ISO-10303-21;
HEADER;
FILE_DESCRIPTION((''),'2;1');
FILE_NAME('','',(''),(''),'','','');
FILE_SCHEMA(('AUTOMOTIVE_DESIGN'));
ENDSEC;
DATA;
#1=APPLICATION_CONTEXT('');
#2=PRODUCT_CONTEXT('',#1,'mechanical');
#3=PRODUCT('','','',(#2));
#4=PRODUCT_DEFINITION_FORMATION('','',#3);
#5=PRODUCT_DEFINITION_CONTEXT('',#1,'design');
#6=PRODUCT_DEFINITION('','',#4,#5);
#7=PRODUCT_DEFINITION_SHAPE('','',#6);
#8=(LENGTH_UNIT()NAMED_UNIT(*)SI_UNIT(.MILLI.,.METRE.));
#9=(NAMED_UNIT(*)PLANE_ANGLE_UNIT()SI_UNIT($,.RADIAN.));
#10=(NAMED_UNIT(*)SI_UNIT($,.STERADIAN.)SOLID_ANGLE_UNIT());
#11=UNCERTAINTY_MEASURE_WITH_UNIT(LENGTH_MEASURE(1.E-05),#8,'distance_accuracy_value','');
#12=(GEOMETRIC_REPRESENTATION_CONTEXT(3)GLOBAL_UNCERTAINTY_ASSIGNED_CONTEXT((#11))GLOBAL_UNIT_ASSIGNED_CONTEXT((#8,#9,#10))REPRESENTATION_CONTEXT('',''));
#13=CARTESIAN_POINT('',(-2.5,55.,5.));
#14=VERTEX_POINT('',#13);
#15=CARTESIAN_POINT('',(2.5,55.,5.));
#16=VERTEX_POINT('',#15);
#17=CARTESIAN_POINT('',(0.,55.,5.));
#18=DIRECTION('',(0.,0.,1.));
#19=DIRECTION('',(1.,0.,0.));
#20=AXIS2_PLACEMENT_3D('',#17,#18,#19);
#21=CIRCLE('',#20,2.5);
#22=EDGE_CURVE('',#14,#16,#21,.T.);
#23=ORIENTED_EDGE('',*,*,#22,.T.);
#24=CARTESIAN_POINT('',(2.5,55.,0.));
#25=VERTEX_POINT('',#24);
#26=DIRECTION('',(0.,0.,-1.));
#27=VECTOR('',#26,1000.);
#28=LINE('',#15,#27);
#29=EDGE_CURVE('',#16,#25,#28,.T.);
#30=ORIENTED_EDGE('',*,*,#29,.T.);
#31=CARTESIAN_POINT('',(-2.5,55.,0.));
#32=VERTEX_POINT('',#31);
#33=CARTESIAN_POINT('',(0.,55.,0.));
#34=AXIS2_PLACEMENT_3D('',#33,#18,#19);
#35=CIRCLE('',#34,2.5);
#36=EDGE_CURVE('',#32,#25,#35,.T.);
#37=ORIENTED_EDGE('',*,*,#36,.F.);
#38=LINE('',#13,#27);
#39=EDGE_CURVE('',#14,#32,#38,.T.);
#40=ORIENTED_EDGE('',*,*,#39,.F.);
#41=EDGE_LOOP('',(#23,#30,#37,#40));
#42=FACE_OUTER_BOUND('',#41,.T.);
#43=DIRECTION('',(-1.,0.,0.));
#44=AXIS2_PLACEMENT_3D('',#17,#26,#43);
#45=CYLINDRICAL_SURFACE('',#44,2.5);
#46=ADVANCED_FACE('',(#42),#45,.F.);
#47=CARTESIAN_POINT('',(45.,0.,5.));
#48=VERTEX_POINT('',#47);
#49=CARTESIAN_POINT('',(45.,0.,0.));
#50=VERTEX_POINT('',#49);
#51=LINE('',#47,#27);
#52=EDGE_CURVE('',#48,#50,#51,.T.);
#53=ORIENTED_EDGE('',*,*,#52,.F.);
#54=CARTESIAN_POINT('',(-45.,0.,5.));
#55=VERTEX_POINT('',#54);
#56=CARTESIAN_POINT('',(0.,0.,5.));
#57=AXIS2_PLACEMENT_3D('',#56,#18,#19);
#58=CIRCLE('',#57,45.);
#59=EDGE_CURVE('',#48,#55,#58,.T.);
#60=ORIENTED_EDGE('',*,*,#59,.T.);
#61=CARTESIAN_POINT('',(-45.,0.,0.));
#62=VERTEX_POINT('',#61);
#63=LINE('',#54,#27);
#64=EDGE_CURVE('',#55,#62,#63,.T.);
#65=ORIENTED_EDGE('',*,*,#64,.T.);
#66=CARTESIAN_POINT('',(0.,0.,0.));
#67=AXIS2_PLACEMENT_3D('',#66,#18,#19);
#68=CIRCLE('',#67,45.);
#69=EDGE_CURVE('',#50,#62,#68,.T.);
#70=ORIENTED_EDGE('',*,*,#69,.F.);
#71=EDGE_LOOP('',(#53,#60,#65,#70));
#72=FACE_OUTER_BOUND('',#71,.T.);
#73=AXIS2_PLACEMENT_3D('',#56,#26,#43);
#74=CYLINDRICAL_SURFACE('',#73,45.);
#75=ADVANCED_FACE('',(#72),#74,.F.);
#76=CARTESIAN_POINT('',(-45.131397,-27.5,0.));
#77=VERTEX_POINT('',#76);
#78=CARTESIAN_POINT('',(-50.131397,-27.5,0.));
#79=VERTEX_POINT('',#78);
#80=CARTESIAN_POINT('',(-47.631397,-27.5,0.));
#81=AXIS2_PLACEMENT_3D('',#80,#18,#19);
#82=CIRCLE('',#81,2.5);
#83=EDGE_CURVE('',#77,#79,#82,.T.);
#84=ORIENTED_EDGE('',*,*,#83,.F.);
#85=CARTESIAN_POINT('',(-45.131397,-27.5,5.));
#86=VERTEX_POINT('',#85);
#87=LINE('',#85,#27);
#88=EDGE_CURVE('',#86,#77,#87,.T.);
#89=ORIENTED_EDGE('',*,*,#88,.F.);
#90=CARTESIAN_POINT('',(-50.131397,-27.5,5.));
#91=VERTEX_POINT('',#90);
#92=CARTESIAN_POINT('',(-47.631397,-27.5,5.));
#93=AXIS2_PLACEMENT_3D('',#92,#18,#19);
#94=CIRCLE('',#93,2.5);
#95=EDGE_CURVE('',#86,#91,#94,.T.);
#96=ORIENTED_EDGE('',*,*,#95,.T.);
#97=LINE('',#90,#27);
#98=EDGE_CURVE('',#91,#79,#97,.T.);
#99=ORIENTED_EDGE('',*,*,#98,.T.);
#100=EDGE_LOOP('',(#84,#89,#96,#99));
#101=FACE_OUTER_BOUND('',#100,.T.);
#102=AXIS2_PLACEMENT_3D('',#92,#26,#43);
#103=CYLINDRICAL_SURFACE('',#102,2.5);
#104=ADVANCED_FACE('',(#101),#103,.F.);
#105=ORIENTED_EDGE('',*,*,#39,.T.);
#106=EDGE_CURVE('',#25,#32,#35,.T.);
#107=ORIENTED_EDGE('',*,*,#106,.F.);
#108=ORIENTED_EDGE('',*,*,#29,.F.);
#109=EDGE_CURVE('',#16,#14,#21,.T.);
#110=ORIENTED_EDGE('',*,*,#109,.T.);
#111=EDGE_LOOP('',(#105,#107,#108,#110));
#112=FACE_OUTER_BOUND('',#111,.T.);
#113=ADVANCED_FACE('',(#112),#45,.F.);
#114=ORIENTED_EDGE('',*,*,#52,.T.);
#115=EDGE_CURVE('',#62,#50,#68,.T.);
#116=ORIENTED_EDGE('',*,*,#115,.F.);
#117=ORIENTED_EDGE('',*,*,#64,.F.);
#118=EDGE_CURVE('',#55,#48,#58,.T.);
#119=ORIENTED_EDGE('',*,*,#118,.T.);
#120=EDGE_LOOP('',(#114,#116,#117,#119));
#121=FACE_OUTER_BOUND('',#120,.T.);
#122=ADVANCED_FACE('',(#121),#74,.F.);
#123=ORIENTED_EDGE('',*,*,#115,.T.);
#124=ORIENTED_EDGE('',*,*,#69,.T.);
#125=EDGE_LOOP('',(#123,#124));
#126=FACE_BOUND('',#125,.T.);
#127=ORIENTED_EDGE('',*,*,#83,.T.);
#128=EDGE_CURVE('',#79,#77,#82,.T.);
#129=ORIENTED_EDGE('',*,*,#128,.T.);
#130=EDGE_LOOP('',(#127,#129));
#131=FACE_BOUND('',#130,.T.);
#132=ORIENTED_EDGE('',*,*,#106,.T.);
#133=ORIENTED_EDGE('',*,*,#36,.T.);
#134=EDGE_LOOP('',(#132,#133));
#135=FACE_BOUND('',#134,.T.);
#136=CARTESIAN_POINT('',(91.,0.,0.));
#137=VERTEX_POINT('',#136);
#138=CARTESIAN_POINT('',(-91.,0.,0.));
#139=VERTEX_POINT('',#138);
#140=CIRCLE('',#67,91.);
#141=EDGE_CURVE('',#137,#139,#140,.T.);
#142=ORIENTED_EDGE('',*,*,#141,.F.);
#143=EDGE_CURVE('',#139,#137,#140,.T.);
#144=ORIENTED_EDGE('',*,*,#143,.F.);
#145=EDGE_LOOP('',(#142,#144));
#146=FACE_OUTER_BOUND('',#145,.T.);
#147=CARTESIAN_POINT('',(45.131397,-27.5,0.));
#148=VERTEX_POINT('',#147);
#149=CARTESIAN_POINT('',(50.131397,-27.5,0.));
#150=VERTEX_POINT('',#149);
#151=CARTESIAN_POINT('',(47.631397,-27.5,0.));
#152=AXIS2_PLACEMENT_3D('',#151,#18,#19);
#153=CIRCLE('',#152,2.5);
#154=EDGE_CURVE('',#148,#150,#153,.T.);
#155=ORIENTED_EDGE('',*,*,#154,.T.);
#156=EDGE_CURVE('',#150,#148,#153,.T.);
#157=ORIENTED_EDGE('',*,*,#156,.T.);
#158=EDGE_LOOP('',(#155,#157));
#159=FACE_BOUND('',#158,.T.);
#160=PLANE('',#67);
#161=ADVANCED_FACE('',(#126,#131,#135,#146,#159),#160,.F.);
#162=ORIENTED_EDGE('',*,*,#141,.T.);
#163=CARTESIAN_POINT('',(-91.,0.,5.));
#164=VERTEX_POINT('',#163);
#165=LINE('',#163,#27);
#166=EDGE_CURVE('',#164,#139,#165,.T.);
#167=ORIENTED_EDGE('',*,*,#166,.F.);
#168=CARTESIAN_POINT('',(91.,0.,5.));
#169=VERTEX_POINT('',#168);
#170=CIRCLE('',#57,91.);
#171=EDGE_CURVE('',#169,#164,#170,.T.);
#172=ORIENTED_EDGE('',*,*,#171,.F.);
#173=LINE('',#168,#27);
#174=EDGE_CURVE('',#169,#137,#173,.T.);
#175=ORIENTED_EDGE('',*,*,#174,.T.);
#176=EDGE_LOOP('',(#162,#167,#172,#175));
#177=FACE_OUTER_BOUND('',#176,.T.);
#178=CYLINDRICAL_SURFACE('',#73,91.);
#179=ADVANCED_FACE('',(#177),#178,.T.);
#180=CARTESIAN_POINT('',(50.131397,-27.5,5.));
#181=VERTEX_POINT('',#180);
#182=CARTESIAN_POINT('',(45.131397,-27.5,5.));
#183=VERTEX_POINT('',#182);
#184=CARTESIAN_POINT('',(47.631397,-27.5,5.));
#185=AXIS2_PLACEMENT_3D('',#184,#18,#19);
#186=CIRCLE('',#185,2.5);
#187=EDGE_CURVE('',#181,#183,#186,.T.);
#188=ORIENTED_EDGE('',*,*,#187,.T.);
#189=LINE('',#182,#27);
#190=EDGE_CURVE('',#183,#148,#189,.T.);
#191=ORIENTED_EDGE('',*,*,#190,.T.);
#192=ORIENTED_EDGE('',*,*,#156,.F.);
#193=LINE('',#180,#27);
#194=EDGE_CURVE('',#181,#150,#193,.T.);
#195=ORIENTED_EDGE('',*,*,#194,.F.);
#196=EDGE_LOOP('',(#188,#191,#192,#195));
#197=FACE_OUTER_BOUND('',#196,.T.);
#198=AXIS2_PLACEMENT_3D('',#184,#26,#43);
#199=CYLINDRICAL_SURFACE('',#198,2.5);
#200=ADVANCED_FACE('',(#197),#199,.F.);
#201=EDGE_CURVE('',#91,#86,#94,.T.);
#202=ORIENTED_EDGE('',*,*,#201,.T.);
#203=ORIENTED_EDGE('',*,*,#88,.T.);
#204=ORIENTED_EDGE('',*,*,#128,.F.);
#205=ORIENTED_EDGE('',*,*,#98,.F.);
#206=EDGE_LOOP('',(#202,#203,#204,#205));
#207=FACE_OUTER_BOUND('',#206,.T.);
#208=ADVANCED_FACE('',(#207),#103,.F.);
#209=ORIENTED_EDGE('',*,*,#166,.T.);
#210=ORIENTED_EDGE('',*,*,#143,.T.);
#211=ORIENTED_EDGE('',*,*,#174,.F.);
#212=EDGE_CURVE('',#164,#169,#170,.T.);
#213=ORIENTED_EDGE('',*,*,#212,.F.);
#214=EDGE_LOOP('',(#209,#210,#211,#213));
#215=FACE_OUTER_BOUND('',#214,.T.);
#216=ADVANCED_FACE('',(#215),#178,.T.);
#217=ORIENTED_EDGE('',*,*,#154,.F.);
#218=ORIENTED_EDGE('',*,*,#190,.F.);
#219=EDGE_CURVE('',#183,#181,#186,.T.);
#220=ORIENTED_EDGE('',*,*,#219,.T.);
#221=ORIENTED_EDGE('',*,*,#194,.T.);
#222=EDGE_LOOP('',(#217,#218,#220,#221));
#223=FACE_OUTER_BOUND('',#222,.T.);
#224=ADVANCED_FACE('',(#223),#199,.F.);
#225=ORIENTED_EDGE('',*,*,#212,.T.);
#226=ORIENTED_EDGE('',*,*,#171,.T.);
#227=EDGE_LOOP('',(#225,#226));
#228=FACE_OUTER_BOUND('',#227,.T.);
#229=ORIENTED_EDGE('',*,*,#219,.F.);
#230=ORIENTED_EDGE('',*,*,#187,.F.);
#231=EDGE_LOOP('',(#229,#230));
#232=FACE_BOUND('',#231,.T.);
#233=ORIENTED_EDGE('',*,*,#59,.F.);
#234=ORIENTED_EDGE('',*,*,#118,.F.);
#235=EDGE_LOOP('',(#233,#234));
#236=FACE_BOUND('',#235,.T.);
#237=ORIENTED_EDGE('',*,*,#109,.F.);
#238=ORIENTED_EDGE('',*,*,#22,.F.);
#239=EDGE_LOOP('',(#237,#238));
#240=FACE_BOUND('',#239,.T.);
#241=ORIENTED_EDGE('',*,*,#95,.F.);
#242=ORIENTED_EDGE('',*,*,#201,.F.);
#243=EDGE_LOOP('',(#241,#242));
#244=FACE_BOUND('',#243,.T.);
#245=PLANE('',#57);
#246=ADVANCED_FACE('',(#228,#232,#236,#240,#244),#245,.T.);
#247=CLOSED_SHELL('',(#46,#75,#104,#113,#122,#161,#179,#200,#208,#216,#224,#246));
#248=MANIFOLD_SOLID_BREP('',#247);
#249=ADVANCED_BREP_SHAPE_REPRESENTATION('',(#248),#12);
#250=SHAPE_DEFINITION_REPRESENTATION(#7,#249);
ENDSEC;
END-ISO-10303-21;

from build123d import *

# Parameters (mm, degrees)
SKETCH1_R           = 91
SKETCH1_R_2         = 45
SKETCH1_R_3         = 2.5
BOSS_EXTRUDE1_DEPTH = 5


with BuildPart() as part:
    # Sketch1 → Boss-Extrude1 (new body)
    with BuildSketch(Plane.XY):
        Circle(SKETCH1_R)
        Circle(SKETCH1_R_2, mode=Mode.SUBTRACT)
        with Locations((0, 55)):
            Circle(SKETCH1_R_3, mode=Mode.SUBTRACT)
        with Locations((47.631397208, -27.5)):
            Circle(SKETCH1_R_3, mode=Mode.SUBTRACT)
        with Locations((-47.631397208, -27.5)):
            Circle(SKETCH1_R_3, mode=Mode.SUBTRACT)
    extrude(amount=BOSS_EXTRUDE1_DEPTH)


solid = part.part
